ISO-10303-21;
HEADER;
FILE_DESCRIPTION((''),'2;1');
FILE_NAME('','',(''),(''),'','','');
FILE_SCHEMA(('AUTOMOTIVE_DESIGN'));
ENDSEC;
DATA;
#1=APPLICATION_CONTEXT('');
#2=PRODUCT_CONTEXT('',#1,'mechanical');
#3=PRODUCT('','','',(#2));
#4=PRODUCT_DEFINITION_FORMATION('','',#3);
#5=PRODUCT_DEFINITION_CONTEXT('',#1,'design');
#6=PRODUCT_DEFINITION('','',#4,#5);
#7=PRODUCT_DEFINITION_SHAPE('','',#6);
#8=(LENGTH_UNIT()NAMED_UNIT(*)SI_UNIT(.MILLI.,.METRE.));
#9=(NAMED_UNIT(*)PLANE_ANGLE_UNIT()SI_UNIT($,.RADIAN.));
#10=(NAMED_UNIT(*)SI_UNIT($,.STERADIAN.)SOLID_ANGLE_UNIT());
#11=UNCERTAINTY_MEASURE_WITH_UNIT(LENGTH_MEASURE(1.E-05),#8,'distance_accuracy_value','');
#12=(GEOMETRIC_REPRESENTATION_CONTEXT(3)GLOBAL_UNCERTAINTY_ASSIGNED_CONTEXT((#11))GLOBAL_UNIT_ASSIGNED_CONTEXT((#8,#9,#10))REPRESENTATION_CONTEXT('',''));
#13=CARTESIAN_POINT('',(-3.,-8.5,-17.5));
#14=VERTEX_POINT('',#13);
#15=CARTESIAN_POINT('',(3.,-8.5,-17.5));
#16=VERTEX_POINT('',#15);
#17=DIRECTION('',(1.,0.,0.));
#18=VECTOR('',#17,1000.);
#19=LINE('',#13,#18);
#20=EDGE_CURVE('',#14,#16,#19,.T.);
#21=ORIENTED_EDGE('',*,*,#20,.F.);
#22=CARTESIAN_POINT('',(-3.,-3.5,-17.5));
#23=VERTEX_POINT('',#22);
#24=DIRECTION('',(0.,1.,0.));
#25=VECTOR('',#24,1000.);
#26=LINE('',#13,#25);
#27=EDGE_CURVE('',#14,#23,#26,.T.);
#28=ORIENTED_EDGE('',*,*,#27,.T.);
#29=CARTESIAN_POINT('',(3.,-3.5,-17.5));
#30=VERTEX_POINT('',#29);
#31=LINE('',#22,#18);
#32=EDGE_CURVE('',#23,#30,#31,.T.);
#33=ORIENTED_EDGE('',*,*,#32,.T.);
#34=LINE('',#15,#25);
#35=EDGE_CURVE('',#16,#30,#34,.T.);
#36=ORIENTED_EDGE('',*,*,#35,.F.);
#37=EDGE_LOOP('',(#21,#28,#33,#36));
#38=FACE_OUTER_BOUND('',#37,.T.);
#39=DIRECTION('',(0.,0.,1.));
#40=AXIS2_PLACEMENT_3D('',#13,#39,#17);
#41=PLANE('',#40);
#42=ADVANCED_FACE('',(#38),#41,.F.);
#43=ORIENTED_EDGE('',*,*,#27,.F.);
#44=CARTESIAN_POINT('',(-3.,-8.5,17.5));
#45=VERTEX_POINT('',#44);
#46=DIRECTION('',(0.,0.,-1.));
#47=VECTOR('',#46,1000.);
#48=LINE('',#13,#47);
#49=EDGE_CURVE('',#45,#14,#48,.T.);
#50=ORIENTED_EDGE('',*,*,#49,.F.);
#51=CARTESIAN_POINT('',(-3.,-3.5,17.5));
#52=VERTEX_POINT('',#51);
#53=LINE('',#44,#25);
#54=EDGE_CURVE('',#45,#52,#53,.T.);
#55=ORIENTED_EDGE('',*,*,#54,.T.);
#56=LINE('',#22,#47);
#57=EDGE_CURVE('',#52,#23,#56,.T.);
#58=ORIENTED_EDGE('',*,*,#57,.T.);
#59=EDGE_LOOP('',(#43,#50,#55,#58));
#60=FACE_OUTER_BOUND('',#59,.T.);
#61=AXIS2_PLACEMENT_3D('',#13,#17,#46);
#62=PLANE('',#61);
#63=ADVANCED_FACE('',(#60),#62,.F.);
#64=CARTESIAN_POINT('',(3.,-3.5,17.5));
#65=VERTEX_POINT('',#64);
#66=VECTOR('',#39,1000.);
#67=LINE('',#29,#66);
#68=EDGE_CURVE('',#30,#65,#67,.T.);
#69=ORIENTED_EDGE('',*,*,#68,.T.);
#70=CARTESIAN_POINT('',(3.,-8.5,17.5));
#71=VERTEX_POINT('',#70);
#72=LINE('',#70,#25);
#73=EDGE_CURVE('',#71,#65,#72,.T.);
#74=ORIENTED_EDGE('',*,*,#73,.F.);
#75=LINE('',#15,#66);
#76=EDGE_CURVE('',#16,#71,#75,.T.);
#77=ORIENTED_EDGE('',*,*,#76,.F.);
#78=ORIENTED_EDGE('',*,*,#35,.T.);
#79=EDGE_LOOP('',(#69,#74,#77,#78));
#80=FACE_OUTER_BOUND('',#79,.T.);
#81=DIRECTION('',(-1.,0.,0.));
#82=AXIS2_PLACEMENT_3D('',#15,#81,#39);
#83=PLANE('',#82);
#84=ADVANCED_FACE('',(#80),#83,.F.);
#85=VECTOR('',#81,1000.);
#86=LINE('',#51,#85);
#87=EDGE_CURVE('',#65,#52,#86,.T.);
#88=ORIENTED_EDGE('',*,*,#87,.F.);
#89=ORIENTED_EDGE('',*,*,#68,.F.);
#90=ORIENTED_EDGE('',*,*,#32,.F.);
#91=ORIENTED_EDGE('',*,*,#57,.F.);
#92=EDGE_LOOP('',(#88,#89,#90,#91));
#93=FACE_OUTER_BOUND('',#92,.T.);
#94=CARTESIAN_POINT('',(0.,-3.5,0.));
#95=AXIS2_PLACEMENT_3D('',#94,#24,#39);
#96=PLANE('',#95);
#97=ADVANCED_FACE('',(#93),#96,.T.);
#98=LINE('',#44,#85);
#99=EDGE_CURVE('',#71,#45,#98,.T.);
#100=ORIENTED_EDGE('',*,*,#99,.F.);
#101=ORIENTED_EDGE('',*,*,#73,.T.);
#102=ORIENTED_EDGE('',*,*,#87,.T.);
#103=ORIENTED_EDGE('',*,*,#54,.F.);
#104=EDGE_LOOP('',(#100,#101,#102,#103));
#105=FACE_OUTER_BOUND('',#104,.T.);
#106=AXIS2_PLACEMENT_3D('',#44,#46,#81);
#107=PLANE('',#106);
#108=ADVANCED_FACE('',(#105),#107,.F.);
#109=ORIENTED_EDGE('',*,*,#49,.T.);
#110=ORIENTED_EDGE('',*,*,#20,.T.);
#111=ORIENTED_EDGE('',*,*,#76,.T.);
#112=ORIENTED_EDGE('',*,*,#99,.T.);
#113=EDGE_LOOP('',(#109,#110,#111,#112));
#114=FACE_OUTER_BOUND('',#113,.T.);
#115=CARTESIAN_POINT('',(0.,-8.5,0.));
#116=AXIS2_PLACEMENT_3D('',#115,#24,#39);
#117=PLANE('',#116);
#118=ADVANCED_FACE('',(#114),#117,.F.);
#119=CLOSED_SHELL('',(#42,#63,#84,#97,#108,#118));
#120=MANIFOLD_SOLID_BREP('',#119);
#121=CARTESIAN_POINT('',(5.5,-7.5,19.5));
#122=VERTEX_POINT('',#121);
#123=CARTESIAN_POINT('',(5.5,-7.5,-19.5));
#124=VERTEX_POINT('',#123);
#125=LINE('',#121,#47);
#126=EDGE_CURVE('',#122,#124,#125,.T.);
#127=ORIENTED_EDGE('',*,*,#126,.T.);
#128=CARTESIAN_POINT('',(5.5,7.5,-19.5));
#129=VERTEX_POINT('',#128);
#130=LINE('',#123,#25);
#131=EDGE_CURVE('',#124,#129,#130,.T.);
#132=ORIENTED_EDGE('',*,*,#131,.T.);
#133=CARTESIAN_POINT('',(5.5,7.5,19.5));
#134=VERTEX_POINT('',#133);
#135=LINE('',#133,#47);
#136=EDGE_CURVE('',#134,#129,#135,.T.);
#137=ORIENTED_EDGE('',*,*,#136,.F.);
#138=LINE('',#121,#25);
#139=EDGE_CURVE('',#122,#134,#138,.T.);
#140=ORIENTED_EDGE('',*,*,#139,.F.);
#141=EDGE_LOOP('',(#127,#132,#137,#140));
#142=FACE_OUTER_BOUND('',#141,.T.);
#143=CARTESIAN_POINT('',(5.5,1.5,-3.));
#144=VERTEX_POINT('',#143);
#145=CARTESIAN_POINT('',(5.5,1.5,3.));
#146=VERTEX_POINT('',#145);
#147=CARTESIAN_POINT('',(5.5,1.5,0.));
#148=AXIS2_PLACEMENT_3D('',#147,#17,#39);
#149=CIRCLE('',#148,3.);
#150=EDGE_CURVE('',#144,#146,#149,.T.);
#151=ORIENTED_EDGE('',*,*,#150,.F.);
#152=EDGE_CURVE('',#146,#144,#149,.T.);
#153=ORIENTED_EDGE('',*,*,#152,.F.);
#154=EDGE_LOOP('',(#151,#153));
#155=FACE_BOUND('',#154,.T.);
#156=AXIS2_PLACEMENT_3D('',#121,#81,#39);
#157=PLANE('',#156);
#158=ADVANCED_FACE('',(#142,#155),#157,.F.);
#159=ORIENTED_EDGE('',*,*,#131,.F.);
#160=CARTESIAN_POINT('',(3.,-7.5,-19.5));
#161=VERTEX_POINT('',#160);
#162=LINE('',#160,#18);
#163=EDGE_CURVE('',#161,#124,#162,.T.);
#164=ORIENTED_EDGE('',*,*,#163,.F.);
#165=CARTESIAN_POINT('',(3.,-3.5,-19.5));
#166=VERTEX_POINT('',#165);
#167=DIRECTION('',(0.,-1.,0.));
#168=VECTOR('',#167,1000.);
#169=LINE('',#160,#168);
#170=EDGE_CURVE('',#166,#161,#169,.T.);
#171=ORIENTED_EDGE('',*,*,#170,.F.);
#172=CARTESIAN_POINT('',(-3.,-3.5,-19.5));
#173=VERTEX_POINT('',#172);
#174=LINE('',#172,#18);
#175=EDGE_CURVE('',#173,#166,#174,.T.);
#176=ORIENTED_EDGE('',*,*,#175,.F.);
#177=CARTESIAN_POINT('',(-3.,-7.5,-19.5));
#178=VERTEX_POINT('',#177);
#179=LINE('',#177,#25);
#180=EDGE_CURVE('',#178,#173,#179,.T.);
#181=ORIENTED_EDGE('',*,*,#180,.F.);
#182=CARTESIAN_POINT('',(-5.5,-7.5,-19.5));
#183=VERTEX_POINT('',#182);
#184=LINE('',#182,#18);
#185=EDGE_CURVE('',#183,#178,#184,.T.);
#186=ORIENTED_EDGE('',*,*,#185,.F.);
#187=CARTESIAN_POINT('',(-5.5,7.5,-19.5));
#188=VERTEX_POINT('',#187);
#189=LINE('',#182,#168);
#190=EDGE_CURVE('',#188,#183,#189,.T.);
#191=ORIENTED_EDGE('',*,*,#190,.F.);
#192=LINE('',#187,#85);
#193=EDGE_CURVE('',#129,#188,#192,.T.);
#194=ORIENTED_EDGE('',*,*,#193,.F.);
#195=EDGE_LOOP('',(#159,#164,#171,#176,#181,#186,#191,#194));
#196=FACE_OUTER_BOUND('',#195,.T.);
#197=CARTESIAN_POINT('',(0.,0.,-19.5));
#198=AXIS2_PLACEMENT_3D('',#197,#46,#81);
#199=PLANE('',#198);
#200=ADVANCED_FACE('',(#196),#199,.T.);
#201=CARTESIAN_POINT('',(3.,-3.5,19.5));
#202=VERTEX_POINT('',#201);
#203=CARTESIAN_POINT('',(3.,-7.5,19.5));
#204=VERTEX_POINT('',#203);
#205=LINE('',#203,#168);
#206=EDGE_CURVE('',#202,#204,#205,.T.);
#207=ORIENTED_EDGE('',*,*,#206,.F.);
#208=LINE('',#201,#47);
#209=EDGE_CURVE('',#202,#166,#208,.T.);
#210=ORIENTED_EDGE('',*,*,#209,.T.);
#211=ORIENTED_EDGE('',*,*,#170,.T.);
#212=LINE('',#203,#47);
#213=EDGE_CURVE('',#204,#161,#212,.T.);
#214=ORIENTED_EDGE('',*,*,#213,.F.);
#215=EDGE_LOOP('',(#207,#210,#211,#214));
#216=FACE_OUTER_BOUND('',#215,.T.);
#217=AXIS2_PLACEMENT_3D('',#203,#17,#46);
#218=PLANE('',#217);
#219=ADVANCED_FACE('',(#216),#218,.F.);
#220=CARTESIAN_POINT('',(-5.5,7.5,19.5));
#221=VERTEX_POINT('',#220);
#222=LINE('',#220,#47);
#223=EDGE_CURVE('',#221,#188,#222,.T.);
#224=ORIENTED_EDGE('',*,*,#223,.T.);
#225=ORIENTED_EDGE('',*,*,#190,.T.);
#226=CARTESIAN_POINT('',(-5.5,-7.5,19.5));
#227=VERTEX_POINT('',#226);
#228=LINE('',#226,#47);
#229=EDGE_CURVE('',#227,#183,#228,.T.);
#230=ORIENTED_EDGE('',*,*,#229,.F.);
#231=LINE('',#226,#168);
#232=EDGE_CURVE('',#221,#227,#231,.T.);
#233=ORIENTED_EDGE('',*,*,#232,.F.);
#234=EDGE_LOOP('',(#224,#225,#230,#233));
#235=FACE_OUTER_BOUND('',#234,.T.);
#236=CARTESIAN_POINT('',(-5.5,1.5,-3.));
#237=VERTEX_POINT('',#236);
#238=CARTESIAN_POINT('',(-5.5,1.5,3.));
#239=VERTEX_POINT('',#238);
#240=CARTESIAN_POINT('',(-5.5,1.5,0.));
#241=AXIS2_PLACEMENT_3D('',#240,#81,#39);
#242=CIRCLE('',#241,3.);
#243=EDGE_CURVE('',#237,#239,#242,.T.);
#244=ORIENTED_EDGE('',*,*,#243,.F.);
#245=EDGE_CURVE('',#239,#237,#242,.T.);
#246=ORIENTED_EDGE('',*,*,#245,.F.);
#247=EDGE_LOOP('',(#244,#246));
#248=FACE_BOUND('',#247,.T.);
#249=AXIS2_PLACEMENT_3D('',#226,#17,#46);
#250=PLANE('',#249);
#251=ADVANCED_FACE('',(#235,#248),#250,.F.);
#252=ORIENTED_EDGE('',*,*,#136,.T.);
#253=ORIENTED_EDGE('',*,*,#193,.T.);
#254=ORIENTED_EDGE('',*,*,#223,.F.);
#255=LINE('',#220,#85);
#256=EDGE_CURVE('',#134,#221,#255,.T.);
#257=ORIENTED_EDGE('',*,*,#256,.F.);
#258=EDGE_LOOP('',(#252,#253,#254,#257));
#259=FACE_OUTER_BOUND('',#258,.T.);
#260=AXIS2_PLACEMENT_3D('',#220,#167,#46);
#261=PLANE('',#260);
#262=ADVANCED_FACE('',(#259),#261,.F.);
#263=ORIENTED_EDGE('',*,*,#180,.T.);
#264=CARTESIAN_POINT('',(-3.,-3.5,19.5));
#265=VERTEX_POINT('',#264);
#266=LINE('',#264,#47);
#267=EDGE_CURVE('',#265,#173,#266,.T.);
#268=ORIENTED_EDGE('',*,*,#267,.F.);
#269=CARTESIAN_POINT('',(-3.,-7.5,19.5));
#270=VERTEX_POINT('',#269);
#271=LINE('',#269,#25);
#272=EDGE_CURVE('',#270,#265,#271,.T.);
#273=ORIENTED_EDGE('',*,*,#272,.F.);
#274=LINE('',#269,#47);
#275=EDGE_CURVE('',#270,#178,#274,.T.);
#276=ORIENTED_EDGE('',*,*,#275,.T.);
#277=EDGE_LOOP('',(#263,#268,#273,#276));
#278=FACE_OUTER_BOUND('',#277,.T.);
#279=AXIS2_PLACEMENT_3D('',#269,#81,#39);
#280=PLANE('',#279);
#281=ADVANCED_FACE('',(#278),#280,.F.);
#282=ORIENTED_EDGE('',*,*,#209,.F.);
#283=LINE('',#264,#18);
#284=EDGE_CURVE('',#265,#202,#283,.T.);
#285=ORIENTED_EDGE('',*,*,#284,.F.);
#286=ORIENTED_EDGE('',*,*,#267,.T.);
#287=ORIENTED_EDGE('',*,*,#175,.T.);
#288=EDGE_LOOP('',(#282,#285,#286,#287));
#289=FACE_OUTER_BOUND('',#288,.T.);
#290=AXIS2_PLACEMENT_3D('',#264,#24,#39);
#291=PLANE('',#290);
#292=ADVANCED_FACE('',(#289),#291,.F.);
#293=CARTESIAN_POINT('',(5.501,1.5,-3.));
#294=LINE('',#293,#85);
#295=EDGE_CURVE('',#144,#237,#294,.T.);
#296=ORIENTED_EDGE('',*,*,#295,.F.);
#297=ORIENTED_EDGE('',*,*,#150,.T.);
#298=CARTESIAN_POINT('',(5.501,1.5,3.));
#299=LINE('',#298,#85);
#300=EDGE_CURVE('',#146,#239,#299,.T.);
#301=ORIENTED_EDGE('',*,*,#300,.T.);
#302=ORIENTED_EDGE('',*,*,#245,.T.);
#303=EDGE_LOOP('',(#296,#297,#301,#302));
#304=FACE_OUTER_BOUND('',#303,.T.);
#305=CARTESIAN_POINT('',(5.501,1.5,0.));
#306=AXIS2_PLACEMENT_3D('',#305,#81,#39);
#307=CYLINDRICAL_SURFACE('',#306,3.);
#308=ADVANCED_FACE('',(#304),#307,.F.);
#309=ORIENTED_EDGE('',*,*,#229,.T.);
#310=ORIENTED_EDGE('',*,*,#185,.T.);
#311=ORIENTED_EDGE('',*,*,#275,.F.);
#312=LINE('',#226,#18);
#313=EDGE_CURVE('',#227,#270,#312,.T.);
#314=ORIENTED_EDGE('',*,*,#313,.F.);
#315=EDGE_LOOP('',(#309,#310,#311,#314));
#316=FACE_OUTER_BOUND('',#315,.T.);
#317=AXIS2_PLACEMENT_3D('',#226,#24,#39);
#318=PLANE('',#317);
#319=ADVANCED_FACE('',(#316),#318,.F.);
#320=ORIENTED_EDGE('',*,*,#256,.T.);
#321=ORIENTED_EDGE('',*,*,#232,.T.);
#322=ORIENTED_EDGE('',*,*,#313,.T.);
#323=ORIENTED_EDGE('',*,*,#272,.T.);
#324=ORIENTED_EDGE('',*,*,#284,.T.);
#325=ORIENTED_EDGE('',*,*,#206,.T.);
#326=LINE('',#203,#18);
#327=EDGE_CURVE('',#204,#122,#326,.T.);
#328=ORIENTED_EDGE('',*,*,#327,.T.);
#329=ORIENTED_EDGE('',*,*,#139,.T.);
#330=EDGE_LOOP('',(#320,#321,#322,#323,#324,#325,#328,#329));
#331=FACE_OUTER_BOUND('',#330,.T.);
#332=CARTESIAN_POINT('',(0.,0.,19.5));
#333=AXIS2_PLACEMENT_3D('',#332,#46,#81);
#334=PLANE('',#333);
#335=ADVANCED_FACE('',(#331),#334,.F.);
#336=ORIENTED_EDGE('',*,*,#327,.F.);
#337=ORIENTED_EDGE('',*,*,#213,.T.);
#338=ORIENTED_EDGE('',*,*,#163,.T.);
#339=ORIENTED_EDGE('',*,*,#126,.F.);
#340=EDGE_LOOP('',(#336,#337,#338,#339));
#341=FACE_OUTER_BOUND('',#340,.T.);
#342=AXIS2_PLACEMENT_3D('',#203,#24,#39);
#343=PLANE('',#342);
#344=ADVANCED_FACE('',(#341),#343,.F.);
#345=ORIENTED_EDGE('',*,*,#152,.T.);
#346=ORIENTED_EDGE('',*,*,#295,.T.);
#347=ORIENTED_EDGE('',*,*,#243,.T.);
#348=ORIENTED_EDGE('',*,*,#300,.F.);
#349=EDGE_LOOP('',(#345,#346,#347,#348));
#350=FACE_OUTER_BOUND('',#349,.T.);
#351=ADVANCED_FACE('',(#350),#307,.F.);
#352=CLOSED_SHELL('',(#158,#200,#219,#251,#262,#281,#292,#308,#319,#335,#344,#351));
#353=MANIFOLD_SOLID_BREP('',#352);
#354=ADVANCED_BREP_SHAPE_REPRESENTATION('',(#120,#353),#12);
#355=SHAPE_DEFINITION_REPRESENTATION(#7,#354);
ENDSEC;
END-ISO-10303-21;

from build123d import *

# Parameters (mm, degrees)
EXTRUDE_1_DEPTH     = 19.5
SKETCH_2_W          = 6
SKETCH_2_H          = 35
EXTRUDE_2_DEPTH     = 5
SKETCH_3_R          = 3
CUT_EXTRUDE_1_DEPTH = 11


with BuildPart() as part:
    # 草图1 → 凸台-拉伸1 (new, symmetric)
    with BuildSketch(Plane.XY):
        Polygon((3, -7.5), (5.5, -7.5), (5.5, 7.5), (-5.5, 7.5), (-5.5, -7.5), (-3, -7.5), (-3, -3.5), (3, -3.5), align=None)
    extrude(amount=EXTRUDE_1_DEPTH, both=True)

    # 草图3 → 切除-拉伸1 (cut)
    with BuildSketch(Plane.ZY.offset(5.5)):
        with Locations((0, 1.5)):
            Circle(SKETCH_3_R)
    extrude(amount=-CUT_EXTRUDE_1_DEPTH, mode=Mode.SUBTRACT)


with BuildPart() as body_2:
    # 草图2 → 凸台-拉伸2 (new body)
    with BuildSketch(Plane.XZ.offset(3.5)):
        Rectangle(SKETCH_2_W, SKETCH_2_H)
    extrude(amount=EXTRUDE_2_DEPTH)


solid = Compound([part.part, body_2.part])
